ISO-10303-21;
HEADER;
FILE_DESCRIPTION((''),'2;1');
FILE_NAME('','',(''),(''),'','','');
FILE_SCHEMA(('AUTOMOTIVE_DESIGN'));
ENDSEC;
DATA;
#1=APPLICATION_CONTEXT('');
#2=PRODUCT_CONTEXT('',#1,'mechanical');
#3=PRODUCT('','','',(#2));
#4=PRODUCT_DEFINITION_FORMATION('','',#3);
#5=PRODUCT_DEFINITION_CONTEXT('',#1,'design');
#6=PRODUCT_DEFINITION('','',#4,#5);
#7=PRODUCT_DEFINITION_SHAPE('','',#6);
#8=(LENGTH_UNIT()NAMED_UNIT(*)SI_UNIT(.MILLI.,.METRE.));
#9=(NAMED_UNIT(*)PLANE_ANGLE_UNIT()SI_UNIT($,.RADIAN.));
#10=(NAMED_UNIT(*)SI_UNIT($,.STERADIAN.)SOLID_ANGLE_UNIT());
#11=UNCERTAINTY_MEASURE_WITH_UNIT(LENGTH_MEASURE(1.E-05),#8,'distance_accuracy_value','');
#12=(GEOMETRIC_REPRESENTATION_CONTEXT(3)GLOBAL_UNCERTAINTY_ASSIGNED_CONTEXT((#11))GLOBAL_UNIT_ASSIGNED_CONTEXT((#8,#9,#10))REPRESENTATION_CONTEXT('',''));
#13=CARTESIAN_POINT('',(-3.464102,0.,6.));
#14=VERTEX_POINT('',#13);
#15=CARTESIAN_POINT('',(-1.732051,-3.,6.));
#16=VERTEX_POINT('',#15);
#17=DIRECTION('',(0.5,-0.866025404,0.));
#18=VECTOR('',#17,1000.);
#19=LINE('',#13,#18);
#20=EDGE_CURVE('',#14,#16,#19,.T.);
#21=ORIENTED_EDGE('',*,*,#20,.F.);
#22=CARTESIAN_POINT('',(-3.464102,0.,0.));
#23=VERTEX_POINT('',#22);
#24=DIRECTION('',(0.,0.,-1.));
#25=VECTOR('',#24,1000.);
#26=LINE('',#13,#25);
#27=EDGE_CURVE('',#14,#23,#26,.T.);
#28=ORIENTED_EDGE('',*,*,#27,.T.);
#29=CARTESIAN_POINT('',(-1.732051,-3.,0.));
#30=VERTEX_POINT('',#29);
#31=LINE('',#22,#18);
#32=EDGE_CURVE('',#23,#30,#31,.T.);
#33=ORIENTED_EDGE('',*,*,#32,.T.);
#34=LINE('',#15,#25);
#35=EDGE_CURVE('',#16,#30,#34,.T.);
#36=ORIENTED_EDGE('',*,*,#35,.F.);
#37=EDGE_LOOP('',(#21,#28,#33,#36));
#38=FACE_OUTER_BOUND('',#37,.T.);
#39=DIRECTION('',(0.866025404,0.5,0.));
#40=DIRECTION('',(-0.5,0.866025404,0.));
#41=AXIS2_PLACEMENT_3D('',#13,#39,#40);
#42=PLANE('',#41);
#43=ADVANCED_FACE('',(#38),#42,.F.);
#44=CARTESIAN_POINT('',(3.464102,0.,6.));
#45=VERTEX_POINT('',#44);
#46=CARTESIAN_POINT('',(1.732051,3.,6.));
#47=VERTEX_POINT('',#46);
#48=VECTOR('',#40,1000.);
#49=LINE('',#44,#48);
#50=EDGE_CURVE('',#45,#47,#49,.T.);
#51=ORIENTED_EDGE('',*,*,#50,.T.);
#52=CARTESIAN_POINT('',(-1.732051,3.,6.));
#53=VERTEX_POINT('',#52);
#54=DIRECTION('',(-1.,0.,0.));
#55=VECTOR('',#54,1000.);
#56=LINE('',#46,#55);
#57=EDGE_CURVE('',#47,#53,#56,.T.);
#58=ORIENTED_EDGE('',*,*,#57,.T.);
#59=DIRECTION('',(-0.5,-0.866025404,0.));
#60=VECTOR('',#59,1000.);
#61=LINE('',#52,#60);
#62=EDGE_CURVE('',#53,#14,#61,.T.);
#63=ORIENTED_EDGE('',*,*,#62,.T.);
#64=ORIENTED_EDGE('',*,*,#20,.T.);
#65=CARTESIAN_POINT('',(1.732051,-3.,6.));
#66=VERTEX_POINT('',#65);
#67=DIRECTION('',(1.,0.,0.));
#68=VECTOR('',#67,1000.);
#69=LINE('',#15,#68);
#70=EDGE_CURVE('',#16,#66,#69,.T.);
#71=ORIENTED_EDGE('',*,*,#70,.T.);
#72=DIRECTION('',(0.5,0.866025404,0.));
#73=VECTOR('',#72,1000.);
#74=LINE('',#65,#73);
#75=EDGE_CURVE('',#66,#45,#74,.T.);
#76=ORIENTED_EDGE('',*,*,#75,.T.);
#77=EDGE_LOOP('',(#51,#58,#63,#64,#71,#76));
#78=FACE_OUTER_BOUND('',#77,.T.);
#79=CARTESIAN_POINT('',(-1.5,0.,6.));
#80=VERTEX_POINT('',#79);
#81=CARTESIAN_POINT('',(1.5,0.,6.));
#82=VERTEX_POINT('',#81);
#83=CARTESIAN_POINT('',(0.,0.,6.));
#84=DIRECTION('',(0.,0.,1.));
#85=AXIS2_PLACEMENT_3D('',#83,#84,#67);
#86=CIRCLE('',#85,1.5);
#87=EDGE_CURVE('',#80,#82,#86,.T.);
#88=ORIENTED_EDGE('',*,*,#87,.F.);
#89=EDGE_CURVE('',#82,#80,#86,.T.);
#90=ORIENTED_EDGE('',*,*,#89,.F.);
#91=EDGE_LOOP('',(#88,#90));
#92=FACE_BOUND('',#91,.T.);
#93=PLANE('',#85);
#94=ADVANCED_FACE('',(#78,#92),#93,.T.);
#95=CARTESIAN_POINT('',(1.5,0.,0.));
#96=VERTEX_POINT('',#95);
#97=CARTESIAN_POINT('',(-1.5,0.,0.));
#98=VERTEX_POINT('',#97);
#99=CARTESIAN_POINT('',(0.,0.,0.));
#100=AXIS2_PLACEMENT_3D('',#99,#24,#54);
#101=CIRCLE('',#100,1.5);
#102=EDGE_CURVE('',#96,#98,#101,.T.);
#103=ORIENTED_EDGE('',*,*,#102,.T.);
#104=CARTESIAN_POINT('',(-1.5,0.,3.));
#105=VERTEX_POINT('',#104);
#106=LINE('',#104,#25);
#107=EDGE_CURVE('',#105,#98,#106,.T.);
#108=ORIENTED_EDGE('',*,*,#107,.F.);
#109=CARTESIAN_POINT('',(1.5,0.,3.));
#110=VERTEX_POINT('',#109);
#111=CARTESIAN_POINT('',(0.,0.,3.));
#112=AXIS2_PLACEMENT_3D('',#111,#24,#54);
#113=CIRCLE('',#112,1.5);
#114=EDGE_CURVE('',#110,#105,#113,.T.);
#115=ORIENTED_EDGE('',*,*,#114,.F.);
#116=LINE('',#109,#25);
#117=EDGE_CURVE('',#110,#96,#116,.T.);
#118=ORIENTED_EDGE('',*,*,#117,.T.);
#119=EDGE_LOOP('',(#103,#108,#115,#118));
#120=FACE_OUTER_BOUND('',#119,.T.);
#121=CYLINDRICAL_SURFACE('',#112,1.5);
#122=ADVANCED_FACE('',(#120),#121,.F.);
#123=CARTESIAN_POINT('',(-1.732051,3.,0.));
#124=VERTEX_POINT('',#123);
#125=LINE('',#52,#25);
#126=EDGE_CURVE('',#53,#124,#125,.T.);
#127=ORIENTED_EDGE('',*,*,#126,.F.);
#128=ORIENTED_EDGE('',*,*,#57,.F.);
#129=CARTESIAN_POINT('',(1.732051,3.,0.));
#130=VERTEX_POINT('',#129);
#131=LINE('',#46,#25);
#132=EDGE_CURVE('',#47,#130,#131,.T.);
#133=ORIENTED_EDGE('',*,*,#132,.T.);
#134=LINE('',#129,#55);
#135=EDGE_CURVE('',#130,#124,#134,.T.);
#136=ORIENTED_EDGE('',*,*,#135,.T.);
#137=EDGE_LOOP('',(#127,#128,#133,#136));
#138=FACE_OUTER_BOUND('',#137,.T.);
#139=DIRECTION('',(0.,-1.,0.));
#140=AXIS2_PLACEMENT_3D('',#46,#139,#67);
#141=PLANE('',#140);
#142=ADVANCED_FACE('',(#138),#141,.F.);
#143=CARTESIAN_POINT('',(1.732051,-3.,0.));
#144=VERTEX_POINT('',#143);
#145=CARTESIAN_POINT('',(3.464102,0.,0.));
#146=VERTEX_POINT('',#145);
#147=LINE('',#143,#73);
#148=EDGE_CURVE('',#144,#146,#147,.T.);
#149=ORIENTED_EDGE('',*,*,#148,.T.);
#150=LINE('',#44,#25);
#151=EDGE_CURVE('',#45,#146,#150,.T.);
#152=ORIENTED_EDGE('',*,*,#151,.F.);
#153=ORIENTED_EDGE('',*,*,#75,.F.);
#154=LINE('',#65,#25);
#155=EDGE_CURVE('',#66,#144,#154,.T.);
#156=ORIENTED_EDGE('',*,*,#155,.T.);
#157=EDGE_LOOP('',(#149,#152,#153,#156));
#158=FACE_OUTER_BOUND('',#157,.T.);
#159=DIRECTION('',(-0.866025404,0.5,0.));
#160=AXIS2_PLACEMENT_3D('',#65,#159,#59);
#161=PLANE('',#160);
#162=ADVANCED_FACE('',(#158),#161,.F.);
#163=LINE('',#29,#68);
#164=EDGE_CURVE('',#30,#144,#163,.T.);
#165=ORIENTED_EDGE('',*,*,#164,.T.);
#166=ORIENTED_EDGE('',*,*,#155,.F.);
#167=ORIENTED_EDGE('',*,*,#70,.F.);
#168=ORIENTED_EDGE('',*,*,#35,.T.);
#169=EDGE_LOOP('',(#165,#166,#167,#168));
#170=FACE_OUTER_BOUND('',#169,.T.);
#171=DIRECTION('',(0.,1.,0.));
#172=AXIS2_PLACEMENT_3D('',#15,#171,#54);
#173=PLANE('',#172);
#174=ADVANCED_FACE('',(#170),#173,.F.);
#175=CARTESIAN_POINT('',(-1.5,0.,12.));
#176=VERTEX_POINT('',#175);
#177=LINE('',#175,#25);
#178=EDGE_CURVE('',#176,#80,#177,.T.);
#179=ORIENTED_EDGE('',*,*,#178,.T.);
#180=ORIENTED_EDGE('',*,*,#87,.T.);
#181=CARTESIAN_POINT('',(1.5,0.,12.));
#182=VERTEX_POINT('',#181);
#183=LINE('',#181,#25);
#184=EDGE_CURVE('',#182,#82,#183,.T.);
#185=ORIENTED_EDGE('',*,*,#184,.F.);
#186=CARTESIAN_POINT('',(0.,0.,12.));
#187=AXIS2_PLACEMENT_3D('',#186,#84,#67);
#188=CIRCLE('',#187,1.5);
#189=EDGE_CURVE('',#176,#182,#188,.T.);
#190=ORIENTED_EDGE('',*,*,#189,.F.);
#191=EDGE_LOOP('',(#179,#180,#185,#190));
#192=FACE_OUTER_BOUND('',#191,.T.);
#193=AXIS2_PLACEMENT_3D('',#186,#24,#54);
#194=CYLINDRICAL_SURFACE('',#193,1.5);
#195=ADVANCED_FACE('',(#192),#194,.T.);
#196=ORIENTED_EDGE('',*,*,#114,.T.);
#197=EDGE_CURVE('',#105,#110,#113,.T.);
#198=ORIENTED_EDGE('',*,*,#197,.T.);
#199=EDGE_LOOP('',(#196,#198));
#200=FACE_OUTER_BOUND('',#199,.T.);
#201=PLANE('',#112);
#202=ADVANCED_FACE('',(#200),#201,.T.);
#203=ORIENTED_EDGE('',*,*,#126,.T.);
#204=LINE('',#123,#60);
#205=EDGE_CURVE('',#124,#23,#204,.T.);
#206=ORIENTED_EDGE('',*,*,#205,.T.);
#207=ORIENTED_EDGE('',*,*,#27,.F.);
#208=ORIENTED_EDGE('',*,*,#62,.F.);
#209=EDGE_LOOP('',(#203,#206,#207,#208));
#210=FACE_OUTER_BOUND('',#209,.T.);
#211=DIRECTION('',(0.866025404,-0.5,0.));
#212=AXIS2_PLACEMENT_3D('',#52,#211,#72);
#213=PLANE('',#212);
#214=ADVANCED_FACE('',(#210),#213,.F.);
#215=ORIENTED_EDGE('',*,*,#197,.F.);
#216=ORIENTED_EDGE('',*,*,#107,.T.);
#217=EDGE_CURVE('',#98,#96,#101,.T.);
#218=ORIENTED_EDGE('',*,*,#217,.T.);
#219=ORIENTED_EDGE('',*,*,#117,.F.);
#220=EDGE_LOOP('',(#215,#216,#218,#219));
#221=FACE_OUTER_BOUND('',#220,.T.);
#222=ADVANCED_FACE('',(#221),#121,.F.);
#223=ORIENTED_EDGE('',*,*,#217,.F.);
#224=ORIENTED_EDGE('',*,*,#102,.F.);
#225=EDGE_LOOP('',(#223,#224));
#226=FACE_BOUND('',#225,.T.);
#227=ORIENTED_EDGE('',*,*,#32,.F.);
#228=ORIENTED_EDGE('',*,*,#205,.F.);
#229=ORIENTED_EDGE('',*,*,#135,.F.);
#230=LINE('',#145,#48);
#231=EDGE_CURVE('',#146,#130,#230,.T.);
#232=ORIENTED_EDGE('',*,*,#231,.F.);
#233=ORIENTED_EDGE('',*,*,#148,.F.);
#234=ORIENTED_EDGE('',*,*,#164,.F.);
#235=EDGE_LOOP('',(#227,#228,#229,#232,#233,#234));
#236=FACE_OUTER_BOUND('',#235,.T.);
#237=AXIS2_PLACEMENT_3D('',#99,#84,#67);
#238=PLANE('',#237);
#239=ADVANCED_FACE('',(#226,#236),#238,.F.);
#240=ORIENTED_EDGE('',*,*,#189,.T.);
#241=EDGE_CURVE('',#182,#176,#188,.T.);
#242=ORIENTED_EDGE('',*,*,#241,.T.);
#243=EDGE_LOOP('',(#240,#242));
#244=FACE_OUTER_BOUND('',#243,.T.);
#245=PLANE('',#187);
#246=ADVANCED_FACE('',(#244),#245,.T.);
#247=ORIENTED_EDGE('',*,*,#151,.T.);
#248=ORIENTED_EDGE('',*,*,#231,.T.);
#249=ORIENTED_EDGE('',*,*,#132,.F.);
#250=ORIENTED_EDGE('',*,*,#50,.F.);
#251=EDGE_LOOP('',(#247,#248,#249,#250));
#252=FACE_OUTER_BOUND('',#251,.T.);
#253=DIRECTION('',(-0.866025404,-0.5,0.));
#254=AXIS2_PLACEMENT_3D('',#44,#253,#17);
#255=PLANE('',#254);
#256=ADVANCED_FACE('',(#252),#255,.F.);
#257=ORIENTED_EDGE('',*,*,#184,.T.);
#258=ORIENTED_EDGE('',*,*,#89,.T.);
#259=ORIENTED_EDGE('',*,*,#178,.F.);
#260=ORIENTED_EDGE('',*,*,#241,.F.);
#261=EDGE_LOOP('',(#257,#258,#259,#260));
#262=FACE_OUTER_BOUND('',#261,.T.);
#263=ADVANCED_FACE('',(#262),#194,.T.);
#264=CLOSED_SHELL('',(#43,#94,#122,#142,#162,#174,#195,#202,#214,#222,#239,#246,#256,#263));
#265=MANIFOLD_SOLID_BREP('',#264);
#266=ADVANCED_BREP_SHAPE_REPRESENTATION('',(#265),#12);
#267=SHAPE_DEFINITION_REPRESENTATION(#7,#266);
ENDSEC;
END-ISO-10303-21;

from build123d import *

# Parameters (mm, degrees)
EXTRUDE_1_DEPTH     = 6
SKETCH_2_R          = 1.5
EXTRUDE_2_DEPTH     = 6
SKETCH_3_R          = 1.5
CUT_EXTRUDE_1_DEPTH = 3


with BuildPart() as part:
    # 草图1 → 凸台-拉伸1 (new body)
    with BuildSketch(Plane.XY):
        Polygon((3.464101615, 0), (1.732050808, 3), (-1.732050808, 3), (-3.464101615, 0), (-1.732050808, -3), (1.732050808, -3), align=None)
    extrude(amount=EXTRUDE_1_DEPTH)

    # 草图2 → 凸台-拉伸2 (add)
    with BuildSketch(Plane.XY.offset(6)):
        Circle(SKETCH_2_R)
    extrude(amount=EXTRUDE_2_DEPTH)

    # 草图3 → 切除-拉伸1 (cut)
    with BuildSketch(Plane(origin=(0, 0, 0), x_dir=(-1, 0, 0), z_dir=(0, 0, -1))):
        with Locations(Location((0, 0, 0), (0, 0, 180))):
            Circle(SKETCH_3_R)
    extrude(amount=-CUT_EXTRUDE_1_DEPTH, mode=Mode.SUBTRACT)


solid = part.part
